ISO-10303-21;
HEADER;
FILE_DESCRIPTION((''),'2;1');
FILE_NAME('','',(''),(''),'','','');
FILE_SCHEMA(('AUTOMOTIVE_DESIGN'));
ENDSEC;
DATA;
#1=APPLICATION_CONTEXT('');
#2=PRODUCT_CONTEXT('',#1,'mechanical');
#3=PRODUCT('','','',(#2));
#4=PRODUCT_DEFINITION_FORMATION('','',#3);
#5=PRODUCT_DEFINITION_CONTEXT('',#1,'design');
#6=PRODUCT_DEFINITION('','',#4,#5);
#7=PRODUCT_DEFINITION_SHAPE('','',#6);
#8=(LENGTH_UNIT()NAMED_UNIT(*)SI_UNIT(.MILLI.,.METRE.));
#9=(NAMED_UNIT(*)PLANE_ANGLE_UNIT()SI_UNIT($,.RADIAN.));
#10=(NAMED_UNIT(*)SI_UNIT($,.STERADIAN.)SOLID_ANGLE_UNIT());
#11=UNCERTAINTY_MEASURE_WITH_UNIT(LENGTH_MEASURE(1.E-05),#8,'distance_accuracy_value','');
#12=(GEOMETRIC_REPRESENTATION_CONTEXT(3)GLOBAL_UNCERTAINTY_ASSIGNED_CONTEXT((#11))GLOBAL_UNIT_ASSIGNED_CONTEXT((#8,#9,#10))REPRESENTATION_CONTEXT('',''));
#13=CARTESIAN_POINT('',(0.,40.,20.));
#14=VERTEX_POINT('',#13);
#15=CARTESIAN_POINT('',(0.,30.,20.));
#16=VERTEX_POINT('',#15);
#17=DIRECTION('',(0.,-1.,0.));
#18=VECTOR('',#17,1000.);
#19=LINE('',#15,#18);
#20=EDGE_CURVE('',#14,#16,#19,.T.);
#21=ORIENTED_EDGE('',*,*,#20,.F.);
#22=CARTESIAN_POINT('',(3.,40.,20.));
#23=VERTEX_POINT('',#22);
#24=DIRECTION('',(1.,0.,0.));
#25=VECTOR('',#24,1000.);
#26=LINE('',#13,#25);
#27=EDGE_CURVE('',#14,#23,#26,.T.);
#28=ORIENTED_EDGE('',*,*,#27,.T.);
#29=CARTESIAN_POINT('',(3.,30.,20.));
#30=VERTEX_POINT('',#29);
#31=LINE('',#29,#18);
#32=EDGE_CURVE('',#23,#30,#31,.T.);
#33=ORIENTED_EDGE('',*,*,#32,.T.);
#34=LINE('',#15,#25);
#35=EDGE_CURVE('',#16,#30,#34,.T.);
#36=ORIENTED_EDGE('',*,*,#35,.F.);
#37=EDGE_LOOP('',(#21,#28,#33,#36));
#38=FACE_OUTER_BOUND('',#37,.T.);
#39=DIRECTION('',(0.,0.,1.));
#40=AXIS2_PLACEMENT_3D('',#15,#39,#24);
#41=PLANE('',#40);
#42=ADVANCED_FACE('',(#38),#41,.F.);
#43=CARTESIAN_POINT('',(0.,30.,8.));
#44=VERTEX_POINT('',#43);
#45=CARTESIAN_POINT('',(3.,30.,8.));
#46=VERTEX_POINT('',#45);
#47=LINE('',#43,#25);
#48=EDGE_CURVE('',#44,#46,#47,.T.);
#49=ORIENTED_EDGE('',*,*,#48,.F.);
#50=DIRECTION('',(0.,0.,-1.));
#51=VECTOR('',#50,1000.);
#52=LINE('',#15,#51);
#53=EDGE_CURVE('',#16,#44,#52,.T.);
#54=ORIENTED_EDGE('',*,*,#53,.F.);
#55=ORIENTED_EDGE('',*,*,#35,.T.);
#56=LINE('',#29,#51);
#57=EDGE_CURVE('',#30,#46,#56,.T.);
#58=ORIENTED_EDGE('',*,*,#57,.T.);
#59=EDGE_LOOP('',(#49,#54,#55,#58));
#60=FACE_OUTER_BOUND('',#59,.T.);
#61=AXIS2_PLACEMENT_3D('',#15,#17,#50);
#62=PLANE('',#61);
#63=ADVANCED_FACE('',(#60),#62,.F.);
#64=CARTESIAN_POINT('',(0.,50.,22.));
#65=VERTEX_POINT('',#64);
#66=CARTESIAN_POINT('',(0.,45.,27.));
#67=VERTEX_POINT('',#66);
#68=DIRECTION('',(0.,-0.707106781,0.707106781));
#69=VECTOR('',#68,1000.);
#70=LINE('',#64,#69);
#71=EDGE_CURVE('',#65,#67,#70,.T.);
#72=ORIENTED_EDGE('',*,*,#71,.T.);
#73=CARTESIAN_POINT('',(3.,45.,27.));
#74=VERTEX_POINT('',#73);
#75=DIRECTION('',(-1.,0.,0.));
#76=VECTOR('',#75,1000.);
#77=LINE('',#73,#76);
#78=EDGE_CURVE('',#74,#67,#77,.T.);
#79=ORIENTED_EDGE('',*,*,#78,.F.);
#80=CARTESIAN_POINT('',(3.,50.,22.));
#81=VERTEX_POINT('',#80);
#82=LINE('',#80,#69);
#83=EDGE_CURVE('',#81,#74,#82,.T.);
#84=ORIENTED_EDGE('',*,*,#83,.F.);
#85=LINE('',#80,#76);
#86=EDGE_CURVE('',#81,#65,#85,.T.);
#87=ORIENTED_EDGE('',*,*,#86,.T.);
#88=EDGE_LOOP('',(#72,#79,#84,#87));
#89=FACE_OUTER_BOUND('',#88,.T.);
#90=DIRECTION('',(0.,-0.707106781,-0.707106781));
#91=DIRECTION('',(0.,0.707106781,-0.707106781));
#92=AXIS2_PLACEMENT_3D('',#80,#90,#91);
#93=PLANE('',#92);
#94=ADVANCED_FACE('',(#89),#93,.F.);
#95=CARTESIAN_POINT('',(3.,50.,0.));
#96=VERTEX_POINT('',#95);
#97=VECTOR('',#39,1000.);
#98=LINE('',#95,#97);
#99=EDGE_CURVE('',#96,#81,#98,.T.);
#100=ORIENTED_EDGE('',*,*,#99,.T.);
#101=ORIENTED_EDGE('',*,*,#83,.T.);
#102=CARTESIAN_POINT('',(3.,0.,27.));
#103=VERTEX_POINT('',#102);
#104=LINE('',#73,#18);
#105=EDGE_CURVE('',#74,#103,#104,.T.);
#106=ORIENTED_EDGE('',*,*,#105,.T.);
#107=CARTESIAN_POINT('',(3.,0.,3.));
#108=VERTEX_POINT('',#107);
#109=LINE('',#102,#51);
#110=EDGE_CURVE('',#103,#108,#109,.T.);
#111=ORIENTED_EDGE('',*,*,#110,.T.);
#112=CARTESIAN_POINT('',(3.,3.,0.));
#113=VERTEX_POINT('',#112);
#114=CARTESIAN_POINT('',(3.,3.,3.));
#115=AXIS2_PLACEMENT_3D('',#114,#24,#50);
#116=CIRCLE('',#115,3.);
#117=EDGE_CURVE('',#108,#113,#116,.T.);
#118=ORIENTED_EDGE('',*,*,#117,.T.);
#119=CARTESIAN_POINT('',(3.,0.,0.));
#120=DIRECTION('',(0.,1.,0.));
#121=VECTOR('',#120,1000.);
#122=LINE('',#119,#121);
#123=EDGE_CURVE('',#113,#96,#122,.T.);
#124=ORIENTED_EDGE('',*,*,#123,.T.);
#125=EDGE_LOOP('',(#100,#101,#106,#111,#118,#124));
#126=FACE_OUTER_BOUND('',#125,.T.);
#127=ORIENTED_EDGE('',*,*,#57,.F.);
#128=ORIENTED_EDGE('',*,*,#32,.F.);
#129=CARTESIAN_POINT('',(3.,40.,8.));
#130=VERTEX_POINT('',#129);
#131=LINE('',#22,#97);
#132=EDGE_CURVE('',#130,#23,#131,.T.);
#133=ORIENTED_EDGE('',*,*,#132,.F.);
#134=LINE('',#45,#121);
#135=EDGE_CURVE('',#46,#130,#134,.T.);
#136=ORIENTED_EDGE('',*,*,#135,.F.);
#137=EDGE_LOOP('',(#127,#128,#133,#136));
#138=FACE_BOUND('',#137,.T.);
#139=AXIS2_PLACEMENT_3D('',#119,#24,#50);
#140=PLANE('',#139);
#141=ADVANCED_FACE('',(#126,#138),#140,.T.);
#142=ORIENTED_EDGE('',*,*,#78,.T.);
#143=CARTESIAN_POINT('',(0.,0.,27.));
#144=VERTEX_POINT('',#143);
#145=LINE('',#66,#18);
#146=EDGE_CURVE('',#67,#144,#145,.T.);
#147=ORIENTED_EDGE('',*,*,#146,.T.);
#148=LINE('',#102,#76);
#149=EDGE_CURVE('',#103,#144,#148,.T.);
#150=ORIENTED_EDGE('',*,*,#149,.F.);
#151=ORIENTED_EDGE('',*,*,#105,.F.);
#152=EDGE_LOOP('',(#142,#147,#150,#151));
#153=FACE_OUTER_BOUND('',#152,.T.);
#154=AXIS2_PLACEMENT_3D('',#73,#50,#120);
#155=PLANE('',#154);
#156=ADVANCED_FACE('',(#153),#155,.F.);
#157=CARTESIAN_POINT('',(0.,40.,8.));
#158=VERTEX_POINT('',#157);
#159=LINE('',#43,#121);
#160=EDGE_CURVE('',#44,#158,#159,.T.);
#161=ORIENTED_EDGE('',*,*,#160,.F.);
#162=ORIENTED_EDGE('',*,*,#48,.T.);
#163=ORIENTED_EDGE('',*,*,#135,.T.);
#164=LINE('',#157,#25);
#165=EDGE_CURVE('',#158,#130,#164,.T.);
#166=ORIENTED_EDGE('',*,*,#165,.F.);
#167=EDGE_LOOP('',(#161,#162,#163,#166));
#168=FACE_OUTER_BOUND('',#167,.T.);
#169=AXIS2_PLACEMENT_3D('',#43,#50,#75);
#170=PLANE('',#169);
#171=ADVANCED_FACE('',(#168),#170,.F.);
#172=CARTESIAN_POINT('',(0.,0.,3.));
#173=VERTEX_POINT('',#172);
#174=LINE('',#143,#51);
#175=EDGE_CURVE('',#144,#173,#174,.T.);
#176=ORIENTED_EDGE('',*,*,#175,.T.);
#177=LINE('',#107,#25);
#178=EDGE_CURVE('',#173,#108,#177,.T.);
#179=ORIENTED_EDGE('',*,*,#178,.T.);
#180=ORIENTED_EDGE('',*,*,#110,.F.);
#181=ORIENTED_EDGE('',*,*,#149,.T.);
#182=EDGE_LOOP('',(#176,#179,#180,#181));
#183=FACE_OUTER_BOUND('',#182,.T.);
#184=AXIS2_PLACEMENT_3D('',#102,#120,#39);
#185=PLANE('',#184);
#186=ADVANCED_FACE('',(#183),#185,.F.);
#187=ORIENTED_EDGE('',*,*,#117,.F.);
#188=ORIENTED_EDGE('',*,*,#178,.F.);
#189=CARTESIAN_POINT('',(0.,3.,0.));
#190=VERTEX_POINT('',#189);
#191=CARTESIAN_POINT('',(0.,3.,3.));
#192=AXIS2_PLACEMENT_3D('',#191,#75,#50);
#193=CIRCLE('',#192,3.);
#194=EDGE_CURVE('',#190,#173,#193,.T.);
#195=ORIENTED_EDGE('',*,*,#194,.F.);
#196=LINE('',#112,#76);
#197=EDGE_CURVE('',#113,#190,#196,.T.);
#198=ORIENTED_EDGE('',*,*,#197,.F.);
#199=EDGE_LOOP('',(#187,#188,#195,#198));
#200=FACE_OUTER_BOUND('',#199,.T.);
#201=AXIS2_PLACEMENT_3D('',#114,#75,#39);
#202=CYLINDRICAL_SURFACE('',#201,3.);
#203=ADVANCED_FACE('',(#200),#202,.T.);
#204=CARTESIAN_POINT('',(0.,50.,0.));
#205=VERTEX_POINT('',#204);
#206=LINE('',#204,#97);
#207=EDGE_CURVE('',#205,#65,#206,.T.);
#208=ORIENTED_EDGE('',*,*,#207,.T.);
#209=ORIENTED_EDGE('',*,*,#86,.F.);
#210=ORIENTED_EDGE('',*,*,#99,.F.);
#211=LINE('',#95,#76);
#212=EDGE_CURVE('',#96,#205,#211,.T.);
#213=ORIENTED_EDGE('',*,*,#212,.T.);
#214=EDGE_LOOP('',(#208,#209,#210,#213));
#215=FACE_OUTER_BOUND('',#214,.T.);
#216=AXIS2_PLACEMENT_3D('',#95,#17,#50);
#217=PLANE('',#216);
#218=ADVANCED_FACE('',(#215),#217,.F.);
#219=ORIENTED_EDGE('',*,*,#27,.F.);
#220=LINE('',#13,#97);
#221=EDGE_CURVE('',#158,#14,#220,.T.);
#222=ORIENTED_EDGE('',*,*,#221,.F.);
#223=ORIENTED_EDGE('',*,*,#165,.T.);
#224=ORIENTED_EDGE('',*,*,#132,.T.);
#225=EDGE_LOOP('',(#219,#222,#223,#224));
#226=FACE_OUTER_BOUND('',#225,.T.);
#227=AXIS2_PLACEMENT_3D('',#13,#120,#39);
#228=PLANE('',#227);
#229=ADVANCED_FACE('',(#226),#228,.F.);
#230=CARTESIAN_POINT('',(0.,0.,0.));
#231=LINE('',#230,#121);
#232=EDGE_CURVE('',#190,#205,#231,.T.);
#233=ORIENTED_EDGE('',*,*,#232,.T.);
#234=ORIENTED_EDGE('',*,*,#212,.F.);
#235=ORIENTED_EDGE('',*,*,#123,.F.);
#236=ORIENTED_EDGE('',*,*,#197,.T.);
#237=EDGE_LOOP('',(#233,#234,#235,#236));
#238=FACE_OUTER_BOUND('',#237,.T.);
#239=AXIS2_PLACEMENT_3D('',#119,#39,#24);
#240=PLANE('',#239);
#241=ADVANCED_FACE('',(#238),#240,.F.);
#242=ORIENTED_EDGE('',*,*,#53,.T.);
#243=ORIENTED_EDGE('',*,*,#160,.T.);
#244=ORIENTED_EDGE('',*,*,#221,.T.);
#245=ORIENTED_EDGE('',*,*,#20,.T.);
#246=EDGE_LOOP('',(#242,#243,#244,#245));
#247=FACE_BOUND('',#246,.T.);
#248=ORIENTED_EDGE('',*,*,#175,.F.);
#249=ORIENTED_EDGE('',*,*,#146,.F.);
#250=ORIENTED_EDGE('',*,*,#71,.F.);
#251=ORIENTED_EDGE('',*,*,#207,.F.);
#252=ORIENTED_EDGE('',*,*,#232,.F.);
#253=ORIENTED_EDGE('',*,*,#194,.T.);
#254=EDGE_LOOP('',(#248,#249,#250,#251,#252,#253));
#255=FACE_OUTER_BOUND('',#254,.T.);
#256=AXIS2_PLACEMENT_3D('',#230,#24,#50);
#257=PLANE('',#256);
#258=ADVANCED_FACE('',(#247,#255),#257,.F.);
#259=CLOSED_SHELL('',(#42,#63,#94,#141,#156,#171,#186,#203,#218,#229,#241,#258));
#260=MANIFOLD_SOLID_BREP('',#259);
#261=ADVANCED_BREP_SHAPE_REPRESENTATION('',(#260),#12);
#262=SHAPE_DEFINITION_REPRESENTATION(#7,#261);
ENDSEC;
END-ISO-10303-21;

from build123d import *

# Parameters (mm, degrees)
EXTRUDE_1_DEPTH     = 3
FILLET_1_R          = 3
SKETCH_2_W          = 12
SKETCH_2_H          = 10
CUT_EXTRUDE_1_DEPTH = 57.903426962


with BuildPart() as part:
    # 草图1 → 凸台-拉伸1 (new body)
    with BuildSketch(Plane(origin=(0, 0, 0), x_dir=(0, 0, -1), z_dir=(1, 0, 0))):
        Polygon((-22, 50), (-27, 45), (-27, 0), (0, 0), (0, 50), align=None)
    extrude(amount=EXTRUDE_1_DEPTH)

    # 圆角1
    fillet_1_edges = [part.edges().sort_by_distance(p)[0] for p in [
        (1.5, 0, 0),
    ]]
    fillet(fillet_1_edges, radius=FILLET_1_R)

    # 草图2 → 切除-拉伸1 (cut, through all)
    with BuildSketch(Plane(origin=(3, 0, 0), x_dir=(0, 0, -1), z_dir=(1, 0, 0))):
        with Locations((-14, 35)):
            Rectangle(SKETCH_2_W, SKETCH_2_H)
    extrude(amount=-CUT_EXTRUDE_1_DEPTH, mode=Mode.SUBTRACT)


solid = part.part
